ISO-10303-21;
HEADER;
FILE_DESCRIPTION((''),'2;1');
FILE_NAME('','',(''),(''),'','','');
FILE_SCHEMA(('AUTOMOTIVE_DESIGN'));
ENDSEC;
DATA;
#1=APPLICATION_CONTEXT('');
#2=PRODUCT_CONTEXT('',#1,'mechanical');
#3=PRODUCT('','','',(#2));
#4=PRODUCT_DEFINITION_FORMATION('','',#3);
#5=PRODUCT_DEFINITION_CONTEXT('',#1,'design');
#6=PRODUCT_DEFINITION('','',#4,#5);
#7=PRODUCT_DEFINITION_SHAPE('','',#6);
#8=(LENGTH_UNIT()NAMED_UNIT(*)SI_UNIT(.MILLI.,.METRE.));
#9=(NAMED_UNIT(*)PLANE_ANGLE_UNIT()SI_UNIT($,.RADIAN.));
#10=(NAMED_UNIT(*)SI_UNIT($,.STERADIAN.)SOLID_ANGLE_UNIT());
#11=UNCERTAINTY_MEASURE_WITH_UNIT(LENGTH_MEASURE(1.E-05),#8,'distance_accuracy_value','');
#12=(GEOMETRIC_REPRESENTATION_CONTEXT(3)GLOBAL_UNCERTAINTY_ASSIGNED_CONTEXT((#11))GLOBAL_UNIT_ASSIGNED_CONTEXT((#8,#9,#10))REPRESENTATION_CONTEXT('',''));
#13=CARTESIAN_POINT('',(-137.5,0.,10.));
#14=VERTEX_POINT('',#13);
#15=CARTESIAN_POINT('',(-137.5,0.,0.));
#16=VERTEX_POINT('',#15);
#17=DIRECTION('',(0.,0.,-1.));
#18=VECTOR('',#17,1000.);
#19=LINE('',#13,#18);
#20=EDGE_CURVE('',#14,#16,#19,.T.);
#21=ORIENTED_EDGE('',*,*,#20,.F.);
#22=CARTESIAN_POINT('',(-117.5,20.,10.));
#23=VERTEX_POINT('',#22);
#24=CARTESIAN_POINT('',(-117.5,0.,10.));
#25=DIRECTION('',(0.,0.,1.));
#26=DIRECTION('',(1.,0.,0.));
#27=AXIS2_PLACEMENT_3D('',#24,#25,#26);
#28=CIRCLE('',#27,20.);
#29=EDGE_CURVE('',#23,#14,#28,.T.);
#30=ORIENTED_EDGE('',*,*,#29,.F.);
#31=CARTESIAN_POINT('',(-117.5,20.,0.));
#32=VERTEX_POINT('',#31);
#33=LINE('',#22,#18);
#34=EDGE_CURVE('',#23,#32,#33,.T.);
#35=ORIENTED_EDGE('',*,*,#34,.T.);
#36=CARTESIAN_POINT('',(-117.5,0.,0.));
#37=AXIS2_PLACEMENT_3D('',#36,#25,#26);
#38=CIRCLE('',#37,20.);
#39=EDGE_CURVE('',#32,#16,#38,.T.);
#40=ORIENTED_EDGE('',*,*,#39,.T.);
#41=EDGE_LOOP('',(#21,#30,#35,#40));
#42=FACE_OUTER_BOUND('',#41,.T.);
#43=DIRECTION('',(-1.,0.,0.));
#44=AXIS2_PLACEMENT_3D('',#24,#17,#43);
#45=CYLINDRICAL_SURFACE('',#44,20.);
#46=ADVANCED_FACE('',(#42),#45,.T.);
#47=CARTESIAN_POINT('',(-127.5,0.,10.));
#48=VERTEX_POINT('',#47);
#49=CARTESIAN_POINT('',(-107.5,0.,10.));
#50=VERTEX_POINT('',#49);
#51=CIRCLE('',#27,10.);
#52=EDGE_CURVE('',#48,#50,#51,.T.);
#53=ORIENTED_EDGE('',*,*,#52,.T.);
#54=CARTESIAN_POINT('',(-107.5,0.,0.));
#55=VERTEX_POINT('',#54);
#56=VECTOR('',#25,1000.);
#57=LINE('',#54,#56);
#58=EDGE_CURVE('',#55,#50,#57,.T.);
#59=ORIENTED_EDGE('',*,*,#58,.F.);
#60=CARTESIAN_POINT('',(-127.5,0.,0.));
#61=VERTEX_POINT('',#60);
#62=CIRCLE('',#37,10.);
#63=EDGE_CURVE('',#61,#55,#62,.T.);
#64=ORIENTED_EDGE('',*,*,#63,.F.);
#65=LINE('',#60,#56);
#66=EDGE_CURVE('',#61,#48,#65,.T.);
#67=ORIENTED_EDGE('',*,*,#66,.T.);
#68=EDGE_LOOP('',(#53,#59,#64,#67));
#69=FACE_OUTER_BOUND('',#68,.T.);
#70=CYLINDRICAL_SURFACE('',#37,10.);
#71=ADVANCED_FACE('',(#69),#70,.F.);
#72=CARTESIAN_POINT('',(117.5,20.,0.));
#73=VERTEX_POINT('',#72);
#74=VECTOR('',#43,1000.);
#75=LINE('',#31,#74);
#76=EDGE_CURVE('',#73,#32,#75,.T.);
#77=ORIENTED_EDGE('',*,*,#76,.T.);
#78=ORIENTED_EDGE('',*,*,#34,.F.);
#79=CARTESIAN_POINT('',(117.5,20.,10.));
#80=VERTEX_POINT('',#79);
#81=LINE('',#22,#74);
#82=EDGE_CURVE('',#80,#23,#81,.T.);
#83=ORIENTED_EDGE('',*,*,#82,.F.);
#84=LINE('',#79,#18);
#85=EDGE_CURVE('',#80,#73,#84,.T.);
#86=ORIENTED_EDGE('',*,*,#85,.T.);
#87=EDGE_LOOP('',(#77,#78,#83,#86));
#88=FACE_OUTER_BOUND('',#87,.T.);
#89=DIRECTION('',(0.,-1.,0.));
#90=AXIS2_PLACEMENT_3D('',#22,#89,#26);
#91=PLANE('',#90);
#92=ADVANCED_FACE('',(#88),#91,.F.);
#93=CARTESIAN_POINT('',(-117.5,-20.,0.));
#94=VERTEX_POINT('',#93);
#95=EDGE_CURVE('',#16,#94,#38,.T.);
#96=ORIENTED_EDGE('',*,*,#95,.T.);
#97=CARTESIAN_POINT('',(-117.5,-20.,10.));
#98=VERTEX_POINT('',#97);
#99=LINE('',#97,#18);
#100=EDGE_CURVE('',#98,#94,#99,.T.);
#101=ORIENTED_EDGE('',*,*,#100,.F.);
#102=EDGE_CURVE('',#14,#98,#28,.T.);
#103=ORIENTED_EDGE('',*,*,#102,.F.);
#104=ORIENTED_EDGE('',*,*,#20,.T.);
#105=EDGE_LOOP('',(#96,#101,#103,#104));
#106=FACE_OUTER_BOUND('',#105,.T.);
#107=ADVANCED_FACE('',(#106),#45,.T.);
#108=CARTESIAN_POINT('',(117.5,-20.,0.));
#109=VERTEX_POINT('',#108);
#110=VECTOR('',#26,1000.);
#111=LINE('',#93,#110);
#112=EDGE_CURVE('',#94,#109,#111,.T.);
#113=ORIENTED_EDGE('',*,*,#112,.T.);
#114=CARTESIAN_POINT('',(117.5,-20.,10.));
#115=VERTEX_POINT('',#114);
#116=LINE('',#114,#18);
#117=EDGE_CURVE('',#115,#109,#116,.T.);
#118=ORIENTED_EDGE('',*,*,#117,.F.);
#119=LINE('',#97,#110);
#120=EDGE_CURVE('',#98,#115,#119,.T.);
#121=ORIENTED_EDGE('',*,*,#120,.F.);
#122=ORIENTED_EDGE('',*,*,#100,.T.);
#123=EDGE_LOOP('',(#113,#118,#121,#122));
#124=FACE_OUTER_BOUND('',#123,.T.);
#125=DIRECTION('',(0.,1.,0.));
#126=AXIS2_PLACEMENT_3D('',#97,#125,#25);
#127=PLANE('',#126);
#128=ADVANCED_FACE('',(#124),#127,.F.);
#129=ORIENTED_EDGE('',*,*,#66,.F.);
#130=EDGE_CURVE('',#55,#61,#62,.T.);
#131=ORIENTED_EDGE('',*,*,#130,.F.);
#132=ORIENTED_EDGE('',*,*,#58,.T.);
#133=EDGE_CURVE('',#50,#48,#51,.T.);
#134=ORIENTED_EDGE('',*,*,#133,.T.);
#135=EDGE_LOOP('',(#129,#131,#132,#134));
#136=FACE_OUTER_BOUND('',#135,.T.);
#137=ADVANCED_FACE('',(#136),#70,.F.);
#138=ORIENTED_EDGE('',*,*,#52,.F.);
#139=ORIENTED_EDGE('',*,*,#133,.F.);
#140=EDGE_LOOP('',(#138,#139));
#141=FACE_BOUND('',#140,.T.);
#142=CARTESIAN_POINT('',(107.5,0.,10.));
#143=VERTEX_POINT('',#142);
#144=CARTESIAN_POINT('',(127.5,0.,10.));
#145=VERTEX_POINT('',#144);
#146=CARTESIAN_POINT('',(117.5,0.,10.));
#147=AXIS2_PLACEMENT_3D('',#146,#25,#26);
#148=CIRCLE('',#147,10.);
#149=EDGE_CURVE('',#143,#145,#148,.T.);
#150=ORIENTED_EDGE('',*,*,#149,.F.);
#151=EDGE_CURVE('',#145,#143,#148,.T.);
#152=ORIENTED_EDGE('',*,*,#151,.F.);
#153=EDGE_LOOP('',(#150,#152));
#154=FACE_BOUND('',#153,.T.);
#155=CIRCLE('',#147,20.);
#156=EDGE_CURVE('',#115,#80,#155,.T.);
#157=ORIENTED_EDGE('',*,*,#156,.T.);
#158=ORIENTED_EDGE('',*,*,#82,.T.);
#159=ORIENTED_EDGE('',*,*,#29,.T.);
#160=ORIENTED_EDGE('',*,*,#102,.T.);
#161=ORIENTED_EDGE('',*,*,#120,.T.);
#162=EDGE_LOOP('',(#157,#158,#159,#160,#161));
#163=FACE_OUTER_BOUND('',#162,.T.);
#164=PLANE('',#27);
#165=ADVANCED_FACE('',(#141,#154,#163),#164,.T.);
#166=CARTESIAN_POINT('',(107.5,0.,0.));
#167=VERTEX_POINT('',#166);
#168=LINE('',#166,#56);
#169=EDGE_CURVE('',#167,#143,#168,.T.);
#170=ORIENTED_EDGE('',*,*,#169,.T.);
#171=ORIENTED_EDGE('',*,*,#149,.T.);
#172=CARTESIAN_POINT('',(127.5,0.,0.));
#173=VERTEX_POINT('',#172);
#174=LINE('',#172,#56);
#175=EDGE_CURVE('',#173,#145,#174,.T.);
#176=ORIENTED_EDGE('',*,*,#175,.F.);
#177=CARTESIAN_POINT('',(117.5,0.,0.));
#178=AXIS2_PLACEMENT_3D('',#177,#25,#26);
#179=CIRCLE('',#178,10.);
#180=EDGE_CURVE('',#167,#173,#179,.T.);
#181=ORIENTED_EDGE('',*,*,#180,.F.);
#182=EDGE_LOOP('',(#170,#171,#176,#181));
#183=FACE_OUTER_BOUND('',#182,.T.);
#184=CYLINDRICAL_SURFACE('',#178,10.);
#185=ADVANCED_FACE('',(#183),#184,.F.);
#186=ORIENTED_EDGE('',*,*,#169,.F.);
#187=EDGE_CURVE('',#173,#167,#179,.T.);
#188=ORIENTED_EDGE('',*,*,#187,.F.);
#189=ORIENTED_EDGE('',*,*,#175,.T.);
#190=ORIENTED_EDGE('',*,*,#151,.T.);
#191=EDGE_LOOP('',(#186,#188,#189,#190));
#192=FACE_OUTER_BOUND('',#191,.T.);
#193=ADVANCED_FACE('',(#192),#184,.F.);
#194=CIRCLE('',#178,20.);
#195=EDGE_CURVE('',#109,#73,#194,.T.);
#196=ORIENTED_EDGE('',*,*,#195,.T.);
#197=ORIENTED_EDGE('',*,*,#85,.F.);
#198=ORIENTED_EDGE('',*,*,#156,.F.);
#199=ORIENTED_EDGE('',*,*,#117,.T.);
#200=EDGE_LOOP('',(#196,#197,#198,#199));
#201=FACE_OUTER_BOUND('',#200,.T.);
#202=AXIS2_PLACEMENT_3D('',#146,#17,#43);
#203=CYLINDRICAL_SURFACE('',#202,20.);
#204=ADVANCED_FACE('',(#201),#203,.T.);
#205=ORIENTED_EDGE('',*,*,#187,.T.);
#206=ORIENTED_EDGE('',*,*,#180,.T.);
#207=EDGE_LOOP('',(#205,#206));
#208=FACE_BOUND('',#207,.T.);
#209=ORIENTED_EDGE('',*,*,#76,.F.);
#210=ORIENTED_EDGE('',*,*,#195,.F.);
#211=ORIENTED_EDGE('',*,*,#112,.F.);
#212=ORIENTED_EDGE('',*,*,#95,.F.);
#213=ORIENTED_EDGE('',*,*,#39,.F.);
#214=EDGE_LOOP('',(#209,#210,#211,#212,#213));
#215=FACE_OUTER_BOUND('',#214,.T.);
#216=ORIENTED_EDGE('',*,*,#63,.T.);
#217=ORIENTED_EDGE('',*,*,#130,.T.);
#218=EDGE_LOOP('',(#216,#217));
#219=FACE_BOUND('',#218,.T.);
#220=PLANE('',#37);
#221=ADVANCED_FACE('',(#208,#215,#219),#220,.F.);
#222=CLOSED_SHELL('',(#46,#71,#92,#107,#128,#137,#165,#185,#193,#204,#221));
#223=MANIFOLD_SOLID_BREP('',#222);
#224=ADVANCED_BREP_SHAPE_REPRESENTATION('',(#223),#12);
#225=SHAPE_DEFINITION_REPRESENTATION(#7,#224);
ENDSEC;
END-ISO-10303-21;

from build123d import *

# Parameters (mm, degrees)
BOSS_EXTRUDE1_DEPTH = 10
SKETCH2_R           = 10
CUT_EXTRUDE1_DEPTH  = 140.306317158


with BuildPart() as part:
    # Sketch1 → Boss-Extrude1 (new body)
    with BuildSketch(Plane.XY):
        with BuildLine():
            Line((-117.5, 20), (117.5, 20))
            ThreePointArc((117.5, 20), (137.5, 0), (117.5, -20))
            Line((117.5, -20), (-117.5, -20))
            ThreePointArc((-117.5, -20), (-137.5, 0), (-117.5, 20))
        make_face()
    extrude(amount=BOSS_EXTRUDE1_DEPTH)

    # Sketch2 → Cut-Extrude1 (cut, through all)
    with BuildSketch(Plane.XY.offset(10)):
        with Locations((-117.5, 0)):
            Circle(SKETCH2_R)
        with Locations((117.5, 0)):
            Circle(SKETCH2_R)
    extrude(amount=-CUT_EXTRUDE1_DEPTH, mode=Mode.SUBTRACT)


solid = part.part
